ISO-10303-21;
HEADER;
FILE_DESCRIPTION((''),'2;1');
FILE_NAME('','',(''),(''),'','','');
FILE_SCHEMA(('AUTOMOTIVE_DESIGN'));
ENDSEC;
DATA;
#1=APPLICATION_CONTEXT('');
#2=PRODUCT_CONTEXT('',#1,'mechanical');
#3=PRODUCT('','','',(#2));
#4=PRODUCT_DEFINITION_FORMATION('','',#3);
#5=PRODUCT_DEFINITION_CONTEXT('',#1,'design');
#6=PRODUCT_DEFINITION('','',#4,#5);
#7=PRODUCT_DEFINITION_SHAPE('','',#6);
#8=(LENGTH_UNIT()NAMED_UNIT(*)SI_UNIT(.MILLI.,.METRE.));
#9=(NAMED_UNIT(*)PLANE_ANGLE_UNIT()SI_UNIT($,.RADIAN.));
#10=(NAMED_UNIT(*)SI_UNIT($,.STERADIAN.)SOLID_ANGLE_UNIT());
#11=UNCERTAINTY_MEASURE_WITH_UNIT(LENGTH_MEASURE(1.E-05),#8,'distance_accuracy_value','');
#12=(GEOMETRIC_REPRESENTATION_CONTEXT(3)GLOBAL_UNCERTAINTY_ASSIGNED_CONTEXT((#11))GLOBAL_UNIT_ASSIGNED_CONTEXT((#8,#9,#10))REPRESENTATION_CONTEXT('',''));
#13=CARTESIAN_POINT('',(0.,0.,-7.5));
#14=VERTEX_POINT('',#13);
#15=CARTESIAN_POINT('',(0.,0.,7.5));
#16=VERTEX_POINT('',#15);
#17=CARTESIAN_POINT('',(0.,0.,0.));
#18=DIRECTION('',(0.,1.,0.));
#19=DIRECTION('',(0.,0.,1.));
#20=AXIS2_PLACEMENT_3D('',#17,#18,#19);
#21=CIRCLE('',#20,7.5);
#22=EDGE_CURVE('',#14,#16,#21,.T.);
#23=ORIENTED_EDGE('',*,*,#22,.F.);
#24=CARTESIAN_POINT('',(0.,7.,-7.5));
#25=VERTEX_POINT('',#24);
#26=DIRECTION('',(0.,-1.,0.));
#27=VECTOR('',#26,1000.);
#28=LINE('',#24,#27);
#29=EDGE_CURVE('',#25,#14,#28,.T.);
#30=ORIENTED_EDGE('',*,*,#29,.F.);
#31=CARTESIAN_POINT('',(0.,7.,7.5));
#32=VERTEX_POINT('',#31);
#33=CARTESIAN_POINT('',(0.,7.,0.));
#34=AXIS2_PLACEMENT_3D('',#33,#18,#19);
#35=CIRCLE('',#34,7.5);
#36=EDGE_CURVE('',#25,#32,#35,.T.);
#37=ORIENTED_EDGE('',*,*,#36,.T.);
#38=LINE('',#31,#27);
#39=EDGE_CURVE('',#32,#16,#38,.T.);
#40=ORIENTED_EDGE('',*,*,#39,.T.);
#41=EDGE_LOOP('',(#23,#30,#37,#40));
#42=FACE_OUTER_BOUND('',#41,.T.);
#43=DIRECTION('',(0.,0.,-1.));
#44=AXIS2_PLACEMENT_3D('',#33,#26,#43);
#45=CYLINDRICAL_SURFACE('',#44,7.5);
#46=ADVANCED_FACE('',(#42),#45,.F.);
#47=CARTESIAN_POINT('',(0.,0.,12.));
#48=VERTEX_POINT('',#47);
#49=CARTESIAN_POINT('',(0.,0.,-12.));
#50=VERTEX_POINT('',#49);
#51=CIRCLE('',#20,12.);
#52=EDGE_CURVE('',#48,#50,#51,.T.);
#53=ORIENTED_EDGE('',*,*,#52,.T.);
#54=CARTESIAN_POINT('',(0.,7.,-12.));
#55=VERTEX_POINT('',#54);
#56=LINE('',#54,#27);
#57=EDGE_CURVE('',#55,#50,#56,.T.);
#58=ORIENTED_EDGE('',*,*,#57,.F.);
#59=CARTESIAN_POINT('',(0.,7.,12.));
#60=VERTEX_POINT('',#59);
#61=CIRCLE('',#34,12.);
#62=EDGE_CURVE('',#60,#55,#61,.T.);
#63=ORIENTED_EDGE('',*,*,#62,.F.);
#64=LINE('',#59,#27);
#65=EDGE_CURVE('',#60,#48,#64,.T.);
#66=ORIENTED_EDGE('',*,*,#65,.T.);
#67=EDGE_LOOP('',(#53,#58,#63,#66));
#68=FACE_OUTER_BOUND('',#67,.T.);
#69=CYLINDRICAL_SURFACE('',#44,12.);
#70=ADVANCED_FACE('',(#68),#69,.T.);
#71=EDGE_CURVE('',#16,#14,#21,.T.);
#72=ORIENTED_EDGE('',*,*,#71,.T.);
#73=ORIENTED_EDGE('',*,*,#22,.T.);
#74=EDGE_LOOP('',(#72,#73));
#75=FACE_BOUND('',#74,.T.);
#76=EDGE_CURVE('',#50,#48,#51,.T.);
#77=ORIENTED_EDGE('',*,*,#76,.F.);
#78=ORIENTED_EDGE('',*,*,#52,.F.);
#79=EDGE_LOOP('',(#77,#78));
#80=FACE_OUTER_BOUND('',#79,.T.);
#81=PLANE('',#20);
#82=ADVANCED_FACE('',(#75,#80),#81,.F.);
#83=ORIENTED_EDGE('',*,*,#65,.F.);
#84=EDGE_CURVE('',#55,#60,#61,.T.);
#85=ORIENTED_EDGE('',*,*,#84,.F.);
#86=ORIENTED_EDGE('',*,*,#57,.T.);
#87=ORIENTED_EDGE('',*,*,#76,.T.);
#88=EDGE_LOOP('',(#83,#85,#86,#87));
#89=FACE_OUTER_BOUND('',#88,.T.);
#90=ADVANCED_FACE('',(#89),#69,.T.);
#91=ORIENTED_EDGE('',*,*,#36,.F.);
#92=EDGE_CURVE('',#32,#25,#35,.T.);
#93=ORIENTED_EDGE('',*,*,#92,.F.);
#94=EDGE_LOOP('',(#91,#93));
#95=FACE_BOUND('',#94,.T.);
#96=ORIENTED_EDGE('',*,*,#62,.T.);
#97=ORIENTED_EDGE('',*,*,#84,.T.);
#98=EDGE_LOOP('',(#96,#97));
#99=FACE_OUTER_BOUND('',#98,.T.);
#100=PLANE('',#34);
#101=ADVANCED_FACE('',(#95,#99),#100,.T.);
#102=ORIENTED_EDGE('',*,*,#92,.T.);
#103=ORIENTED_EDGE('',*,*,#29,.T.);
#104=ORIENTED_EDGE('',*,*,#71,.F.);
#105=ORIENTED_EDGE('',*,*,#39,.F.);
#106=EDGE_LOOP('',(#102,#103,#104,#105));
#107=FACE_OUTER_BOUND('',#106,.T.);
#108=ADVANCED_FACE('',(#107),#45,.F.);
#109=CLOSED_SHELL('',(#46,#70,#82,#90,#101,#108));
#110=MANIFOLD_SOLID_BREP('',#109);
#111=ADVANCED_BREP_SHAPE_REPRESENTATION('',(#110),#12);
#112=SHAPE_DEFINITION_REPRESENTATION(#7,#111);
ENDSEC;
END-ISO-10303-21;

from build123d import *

# Parameters (mm, degrees)
SKETCH2_R           = 12
SKETCH2_R_2         = 7.5
BOSS_EXTRUDE1_DEPTH = 7


with BuildPart() as part:
    # Sketch2 → Boss-Extrude1 (new body)
    with BuildSketch(Plane(origin=(0, 0, 0), x_dir=(1, 0, 0), z_dir=(0, 1, 0))):
        with Locations(Location((0, 0, 0), (0, 0, 270))):
            Circle(SKETCH2_R)
        with Locations(Location((0, 0, 0), (0, 0, 270))):
            Circle(SKETCH2_R_2, mode=Mode.SUBTRACT)
    extrude(amount=BOSS_EXTRUDE1_DEPTH)


solid = part.part
